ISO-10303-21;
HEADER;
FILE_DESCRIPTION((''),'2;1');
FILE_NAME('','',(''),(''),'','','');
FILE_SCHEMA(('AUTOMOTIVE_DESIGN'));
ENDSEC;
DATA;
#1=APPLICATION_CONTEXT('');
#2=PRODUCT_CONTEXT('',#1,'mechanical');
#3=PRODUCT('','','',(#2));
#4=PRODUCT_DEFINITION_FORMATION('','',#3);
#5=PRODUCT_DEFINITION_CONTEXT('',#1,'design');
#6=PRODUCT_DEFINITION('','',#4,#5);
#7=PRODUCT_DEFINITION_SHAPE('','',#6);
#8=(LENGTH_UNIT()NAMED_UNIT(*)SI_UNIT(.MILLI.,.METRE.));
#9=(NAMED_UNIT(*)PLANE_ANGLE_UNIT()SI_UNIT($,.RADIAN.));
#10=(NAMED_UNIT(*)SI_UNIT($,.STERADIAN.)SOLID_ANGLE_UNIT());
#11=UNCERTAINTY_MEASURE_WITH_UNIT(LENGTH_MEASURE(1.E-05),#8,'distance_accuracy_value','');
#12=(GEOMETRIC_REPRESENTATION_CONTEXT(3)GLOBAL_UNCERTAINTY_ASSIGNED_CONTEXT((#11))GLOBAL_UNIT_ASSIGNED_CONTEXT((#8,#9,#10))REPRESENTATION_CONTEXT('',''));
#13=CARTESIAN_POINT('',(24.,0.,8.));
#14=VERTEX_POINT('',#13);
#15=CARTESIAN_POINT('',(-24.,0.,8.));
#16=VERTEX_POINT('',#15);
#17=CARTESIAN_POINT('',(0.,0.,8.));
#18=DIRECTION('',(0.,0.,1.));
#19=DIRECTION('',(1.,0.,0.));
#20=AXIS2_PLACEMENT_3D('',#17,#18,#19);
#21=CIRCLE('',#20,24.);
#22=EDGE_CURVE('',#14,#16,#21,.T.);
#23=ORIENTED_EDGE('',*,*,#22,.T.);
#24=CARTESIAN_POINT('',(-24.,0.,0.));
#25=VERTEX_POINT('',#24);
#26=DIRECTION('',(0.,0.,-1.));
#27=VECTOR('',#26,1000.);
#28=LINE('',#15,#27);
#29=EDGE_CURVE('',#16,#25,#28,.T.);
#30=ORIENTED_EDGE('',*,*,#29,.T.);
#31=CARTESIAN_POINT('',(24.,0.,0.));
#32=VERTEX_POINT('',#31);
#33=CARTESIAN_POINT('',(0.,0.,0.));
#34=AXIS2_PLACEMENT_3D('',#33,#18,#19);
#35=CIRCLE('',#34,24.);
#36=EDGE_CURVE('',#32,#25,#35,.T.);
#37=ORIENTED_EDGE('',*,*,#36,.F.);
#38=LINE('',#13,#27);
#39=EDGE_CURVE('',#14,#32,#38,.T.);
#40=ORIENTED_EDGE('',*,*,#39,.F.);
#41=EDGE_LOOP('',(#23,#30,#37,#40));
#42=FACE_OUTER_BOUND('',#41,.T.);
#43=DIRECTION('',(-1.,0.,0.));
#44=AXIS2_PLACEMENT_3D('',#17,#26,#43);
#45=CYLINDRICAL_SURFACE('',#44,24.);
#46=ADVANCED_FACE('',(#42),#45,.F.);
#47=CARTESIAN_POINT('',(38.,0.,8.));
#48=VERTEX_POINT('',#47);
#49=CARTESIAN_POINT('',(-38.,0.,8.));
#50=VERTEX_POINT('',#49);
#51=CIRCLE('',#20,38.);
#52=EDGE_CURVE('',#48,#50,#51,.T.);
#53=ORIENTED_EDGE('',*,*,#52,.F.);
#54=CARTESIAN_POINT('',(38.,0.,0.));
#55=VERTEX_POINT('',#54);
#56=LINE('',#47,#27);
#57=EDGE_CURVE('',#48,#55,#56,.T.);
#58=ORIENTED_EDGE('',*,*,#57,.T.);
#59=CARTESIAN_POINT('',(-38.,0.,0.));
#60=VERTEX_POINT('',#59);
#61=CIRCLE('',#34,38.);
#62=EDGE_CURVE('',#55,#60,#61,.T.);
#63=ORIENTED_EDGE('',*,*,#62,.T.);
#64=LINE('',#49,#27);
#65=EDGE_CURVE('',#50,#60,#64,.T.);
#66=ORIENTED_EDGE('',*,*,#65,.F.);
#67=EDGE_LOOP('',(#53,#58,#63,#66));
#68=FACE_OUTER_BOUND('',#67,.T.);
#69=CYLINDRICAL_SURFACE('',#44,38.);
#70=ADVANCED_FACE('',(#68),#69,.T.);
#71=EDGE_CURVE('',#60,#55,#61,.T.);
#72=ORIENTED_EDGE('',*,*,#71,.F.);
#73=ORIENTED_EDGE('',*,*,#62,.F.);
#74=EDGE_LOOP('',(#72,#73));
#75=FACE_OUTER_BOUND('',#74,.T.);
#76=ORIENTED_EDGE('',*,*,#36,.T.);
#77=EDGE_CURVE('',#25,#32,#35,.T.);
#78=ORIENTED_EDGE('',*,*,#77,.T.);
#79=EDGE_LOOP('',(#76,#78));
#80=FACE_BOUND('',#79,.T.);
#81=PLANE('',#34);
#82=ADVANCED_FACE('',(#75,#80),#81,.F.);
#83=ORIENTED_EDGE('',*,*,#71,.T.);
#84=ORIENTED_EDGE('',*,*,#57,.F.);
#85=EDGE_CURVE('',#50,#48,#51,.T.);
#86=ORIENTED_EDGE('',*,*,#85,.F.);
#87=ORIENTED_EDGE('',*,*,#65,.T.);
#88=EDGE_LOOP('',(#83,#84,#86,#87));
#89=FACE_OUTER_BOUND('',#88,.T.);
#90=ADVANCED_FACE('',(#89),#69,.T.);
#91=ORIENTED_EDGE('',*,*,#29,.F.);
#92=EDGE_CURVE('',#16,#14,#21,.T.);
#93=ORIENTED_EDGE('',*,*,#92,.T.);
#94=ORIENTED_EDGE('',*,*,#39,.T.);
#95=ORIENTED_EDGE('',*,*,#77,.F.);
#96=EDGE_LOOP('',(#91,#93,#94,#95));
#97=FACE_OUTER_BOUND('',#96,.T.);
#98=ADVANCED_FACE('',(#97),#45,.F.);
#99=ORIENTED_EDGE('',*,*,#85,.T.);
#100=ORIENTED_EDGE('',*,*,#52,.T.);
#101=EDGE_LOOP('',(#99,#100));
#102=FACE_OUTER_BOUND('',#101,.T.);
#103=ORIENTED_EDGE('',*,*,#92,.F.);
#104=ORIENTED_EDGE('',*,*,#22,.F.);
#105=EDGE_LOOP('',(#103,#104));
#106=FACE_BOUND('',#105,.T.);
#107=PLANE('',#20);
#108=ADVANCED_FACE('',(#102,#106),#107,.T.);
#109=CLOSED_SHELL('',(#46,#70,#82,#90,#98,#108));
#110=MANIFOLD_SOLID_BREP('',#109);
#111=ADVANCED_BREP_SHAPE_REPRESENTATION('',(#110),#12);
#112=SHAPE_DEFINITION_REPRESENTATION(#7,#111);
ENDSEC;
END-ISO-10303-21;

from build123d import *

# Parameters (mm, degrees)
SKETCH1_R           = 38
SKETCH1_R_2         = 24
BOSS_EXTRUDE1_DEPTH = 8


with BuildPart() as part:
    # Sketch1 → Boss-Extrude1 (new body)
    with BuildSketch(Plane.XY):
        Circle(SKETCH1_R)
        Circle(SKETCH1_R_2, mode=Mode.SUBTRACT)
    extrude(amount=BOSS_EXTRUDE1_DEPTH)


solid = part.part
